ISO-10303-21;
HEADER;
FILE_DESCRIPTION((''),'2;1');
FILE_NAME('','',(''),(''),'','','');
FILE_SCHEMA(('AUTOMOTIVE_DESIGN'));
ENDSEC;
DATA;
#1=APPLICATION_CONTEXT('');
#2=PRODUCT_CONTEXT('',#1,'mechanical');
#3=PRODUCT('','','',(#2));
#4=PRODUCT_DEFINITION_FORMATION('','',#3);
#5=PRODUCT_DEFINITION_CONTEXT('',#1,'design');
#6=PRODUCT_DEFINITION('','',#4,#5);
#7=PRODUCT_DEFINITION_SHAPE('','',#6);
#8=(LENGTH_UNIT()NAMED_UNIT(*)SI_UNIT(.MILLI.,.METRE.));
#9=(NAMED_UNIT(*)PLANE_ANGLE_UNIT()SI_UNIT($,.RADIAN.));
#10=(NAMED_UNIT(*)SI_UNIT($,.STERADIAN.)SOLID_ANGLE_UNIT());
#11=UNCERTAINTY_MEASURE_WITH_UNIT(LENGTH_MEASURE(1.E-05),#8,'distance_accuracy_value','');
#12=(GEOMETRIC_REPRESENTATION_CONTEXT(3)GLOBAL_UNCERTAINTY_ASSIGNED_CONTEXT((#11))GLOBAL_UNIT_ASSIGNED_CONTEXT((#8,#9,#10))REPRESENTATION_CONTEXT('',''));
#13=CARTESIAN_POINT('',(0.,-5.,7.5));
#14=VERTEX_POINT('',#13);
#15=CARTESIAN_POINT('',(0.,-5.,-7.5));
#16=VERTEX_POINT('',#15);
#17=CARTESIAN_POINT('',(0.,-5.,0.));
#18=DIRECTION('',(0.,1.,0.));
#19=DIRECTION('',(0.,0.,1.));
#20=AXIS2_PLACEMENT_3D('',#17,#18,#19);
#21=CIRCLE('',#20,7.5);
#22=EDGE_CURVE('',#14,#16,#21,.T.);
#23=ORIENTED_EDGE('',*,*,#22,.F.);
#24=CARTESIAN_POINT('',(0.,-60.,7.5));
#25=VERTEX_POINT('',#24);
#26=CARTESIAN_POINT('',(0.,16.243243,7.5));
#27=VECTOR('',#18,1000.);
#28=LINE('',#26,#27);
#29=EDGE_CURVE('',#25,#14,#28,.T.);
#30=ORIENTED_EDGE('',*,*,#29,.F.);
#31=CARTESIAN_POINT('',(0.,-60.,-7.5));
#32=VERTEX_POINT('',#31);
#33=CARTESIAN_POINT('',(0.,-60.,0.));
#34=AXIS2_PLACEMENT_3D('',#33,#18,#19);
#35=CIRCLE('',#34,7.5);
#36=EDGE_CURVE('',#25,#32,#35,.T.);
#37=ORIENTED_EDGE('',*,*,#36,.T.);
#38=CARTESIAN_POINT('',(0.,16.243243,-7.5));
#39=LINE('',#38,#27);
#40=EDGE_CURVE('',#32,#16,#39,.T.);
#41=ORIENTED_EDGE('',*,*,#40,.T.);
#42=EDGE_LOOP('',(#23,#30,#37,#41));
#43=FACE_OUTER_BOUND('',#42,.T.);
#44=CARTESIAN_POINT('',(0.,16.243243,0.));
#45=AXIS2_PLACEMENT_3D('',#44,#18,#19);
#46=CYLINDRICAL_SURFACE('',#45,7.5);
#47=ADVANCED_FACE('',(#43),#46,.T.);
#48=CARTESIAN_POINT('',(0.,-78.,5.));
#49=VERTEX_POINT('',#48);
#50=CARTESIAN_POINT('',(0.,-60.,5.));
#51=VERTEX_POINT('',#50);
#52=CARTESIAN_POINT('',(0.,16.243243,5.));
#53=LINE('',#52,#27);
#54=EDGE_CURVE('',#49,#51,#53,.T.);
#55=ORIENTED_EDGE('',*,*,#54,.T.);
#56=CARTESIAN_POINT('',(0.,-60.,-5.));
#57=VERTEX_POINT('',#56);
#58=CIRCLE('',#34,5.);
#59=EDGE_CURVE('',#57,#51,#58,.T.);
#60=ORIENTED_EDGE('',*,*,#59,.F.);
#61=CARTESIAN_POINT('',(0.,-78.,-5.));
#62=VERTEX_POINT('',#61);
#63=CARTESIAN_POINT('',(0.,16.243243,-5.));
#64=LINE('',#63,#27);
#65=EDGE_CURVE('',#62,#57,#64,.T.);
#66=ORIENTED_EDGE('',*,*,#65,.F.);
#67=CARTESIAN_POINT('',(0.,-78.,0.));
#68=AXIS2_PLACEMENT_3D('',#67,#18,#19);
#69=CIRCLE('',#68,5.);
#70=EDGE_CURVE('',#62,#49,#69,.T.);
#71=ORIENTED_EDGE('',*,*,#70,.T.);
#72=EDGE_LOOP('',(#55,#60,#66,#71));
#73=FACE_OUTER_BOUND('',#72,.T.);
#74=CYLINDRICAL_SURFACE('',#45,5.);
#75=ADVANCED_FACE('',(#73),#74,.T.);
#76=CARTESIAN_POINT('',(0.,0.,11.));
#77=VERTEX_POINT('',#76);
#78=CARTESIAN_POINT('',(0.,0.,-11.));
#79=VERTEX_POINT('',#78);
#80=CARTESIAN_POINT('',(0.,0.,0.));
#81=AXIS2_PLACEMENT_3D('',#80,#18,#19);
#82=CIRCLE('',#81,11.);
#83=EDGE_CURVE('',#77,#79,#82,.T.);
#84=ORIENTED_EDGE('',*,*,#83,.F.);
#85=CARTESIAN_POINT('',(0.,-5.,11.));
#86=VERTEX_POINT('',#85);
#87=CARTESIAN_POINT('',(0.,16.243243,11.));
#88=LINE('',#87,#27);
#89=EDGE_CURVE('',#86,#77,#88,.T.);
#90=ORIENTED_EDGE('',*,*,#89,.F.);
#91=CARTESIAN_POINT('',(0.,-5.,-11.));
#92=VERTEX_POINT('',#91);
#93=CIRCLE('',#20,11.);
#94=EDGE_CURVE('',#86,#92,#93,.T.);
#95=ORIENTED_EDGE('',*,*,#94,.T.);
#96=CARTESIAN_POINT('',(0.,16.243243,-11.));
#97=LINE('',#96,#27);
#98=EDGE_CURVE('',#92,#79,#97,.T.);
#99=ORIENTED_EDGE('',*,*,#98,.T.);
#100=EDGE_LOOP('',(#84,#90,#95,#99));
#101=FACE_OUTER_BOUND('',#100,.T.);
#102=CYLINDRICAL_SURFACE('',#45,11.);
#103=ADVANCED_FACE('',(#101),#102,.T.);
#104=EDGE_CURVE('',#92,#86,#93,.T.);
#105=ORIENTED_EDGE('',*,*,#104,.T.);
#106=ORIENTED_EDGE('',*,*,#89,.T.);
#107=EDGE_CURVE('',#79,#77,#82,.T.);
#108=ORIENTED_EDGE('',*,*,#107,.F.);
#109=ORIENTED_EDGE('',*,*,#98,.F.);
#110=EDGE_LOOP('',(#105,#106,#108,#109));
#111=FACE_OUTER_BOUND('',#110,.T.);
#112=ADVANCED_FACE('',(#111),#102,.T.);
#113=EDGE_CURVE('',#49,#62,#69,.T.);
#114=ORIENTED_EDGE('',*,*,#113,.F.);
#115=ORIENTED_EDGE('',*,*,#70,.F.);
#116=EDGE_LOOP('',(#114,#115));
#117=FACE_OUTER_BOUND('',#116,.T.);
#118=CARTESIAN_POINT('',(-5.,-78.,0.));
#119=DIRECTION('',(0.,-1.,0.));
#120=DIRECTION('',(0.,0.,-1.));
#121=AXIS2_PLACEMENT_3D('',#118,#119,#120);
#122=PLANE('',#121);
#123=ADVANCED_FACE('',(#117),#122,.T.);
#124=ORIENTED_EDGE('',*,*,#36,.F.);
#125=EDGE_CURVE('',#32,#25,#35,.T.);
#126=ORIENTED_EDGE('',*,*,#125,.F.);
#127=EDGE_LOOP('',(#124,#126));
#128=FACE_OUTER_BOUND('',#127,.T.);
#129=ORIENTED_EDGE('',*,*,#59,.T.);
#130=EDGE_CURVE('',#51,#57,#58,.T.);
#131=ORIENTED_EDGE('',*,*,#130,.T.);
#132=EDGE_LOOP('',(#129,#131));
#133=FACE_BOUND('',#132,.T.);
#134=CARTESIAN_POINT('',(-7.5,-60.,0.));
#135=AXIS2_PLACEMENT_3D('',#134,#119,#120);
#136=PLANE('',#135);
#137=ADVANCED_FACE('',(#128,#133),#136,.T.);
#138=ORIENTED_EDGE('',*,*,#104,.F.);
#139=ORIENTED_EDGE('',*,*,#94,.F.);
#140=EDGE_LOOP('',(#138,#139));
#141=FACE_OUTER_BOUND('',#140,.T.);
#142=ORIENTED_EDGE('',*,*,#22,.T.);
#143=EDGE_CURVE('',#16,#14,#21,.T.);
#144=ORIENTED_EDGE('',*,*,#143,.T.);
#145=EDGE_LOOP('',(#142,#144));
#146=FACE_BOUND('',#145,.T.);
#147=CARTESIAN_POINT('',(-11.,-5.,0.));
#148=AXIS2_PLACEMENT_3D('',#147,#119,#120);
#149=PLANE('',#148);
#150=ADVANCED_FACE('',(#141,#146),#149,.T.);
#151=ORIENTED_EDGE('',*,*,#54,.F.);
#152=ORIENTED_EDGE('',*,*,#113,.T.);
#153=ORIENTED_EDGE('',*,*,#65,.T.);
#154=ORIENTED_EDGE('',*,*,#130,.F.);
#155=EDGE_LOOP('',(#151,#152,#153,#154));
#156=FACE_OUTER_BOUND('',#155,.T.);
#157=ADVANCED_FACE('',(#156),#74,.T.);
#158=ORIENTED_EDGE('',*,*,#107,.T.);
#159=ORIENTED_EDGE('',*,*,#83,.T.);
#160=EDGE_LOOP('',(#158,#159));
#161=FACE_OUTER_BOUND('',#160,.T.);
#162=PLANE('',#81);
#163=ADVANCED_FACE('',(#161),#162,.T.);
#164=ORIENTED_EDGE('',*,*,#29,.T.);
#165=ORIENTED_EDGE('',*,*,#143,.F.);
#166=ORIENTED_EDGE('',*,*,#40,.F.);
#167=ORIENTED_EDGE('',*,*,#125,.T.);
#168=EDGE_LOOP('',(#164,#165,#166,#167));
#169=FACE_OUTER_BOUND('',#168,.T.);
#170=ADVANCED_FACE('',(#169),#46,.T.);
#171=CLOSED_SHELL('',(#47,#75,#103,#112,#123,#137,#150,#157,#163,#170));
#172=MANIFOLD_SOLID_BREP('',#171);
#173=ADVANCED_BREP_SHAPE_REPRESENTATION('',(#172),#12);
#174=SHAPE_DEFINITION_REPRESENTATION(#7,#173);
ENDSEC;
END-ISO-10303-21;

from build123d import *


with BuildPart() as part:
    # Pin Profile Sketch → Pin Body Revolve (revolve)
    with BuildSketch(Plane.XY, mode=Mode.PRIVATE) as pin_body_revolve_sk:
        Polygon((0, 0), (-11, 0), (-11, -5), (-7.5, -5), (-7.5, -60), (-5, -60), (-5, -78), (0, -78), align=None)
    revolve(pin_body_revolve_sk.sketch.rotate(Axis((0, 16.243243243, 0), (0, -1, 0)), 270), axis=Axis((0, 16.243243243, 0), (0, -1, 0)))


solid = part.part
